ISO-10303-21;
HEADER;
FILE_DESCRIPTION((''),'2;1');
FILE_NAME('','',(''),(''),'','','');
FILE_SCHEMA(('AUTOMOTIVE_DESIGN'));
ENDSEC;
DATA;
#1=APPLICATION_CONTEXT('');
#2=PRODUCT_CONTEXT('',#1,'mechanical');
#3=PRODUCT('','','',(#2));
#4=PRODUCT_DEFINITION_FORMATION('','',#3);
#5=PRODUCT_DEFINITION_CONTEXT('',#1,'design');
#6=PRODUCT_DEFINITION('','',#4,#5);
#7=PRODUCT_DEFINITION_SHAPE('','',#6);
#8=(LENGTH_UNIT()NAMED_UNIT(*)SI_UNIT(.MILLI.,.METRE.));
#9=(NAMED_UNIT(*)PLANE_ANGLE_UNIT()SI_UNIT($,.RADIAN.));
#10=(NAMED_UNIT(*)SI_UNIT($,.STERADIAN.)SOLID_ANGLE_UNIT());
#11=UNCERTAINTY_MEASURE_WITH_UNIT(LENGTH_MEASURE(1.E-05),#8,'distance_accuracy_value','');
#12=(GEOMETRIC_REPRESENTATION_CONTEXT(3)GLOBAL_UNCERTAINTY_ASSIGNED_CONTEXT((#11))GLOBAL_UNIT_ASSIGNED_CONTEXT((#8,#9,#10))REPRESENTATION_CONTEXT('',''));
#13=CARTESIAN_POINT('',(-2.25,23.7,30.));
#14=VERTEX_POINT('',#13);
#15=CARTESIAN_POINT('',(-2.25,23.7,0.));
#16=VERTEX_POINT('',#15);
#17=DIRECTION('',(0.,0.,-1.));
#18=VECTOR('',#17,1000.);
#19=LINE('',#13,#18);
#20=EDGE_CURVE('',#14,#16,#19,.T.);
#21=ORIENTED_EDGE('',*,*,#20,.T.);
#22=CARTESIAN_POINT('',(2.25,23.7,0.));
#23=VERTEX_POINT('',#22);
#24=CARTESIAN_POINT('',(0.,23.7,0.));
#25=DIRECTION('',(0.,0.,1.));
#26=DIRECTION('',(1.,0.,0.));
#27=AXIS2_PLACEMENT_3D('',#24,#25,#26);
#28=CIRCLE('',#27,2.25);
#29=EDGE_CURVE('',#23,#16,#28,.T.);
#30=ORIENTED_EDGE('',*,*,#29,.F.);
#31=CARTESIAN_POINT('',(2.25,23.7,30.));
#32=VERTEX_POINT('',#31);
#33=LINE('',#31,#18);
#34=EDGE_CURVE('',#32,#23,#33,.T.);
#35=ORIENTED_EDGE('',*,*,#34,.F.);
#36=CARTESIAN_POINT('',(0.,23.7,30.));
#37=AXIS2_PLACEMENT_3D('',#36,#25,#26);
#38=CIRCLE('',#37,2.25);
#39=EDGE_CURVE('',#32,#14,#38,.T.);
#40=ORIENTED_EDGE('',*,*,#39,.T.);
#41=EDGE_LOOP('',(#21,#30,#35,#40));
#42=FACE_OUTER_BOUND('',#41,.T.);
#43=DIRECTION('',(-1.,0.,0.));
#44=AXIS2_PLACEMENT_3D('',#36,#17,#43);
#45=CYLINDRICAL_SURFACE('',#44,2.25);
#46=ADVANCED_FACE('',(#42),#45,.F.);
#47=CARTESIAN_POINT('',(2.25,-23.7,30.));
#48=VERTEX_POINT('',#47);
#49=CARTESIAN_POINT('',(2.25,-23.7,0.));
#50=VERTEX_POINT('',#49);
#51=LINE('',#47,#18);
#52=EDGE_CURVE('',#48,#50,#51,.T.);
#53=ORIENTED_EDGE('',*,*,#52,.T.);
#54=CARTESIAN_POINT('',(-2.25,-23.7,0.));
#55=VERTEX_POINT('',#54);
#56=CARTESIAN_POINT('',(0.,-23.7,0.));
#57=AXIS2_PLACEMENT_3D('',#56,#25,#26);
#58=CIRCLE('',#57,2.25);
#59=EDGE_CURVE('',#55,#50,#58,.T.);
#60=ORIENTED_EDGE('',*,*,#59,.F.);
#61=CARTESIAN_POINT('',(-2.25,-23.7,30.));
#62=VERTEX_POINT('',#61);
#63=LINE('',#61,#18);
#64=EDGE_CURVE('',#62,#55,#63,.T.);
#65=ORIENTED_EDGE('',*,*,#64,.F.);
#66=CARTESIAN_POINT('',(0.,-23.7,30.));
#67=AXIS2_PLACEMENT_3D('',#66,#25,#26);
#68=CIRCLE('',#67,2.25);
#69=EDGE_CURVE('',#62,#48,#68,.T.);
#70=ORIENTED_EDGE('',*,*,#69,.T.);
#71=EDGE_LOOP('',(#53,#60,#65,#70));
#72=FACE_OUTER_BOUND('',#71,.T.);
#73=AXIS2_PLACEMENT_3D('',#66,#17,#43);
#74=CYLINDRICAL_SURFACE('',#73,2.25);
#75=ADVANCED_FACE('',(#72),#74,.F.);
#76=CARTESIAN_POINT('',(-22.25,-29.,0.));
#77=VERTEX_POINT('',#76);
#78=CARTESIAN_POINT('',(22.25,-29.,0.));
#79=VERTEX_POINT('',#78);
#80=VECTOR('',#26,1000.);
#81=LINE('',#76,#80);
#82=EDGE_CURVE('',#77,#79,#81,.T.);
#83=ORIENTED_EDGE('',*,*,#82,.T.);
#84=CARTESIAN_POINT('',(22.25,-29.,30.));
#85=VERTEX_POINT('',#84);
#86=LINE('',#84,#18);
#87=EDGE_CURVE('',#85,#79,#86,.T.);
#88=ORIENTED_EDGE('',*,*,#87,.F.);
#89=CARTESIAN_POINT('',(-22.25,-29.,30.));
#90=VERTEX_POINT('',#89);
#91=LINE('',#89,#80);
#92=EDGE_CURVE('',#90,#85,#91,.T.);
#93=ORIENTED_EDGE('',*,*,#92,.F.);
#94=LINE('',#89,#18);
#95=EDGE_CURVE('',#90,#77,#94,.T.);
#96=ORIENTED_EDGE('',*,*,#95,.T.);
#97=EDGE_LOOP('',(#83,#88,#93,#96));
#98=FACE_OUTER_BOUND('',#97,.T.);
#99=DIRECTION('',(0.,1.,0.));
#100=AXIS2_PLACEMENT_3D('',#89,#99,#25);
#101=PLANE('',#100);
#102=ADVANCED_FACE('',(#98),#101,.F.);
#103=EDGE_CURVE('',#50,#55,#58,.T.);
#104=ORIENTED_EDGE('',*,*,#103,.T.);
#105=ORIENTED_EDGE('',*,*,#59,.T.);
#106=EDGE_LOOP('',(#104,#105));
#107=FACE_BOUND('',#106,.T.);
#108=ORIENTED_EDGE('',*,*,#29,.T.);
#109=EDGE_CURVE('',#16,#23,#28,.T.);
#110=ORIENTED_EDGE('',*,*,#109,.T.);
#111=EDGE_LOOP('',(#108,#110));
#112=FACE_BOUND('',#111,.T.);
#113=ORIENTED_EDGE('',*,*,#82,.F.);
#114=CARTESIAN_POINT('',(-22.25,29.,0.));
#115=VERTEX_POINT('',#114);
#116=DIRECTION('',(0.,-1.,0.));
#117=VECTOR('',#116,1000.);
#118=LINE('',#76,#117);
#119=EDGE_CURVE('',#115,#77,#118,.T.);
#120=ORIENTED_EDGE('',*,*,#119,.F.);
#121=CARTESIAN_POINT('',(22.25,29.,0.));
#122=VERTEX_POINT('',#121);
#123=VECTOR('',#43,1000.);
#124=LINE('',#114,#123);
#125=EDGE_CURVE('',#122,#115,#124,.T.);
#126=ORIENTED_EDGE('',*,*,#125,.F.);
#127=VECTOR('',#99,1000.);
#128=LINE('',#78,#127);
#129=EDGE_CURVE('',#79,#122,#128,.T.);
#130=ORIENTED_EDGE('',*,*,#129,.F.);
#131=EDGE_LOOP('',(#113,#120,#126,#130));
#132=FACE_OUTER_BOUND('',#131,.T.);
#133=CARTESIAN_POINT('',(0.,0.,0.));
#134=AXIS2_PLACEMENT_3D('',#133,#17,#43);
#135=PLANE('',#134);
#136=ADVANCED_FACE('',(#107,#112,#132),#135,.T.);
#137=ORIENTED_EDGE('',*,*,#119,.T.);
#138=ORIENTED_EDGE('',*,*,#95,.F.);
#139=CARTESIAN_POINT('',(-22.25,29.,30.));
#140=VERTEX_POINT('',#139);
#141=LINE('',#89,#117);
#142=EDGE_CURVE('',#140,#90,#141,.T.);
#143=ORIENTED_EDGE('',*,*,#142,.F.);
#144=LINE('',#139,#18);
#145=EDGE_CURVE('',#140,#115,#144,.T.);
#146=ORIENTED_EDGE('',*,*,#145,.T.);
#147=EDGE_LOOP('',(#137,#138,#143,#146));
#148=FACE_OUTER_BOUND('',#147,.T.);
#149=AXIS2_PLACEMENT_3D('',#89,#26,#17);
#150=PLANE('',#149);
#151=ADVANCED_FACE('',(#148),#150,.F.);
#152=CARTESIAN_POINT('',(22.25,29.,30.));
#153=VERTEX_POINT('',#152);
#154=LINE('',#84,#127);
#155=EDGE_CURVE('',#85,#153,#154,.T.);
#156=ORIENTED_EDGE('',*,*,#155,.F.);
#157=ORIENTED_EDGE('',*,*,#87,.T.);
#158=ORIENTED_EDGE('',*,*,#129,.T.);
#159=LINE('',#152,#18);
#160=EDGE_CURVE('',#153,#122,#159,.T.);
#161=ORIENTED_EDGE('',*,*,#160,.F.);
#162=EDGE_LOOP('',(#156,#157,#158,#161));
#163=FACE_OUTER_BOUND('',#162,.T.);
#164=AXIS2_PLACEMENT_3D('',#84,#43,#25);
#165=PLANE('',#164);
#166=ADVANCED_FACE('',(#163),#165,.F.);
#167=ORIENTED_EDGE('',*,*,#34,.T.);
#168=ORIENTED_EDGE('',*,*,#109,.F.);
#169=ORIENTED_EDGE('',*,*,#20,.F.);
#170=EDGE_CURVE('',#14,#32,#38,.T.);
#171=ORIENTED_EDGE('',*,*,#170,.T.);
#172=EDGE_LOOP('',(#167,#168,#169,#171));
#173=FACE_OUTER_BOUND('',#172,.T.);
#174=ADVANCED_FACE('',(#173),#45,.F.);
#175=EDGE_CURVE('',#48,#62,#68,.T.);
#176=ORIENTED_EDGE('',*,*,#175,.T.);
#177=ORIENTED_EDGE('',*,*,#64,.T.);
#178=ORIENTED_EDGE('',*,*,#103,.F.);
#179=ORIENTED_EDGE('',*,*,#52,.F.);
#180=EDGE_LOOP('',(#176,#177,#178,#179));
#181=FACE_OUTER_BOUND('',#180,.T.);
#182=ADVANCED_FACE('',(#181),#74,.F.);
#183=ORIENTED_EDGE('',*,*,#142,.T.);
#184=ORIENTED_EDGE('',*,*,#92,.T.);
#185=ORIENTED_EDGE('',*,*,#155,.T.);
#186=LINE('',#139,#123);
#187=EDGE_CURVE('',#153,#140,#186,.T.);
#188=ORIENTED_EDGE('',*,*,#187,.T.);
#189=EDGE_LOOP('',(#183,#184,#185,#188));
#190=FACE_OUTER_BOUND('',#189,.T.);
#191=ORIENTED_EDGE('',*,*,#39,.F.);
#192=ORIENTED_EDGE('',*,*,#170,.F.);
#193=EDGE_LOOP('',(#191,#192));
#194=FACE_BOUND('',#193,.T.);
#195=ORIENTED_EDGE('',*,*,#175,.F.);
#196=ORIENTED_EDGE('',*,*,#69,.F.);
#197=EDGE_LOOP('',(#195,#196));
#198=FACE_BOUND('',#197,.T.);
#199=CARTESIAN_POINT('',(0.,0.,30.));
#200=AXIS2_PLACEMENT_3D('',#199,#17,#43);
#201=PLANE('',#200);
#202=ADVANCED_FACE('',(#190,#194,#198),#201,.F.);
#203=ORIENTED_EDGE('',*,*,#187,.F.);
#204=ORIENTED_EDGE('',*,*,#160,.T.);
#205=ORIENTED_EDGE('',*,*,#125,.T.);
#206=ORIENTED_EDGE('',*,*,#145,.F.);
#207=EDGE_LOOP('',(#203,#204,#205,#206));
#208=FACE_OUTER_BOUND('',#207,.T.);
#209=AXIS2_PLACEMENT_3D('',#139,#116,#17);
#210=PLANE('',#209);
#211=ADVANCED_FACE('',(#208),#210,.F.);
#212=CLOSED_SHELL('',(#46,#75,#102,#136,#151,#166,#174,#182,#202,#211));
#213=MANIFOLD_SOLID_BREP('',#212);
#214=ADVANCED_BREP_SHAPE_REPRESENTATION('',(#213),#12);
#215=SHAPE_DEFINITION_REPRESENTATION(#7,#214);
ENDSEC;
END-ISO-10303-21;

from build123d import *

# Parameters (mm, degrees)
SKETCH_1_W      = 44.5
SKETCH_1_H      = 58
SKETCH_1_R      = 2.25
EXTRUDE_1_DEPTH = 30


with BuildPart() as part:
    # 草图1 → 凸台-拉伸1 (new body)
    with BuildSketch(Plane.XY):
        Rectangle(SKETCH_1_W, SKETCH_1_H)
        with Locations((0, 23.7)):
            Circle(SKETCH_1_R, mode=Mode.SUBTRACT)
        with Locations((0, -23.7)):
            Circle(SKETCH_1_R, mode=Mode.SUBTRACT)
    extrude(amount=EXTRUDE_1_DEPTH)


solid = part.part
